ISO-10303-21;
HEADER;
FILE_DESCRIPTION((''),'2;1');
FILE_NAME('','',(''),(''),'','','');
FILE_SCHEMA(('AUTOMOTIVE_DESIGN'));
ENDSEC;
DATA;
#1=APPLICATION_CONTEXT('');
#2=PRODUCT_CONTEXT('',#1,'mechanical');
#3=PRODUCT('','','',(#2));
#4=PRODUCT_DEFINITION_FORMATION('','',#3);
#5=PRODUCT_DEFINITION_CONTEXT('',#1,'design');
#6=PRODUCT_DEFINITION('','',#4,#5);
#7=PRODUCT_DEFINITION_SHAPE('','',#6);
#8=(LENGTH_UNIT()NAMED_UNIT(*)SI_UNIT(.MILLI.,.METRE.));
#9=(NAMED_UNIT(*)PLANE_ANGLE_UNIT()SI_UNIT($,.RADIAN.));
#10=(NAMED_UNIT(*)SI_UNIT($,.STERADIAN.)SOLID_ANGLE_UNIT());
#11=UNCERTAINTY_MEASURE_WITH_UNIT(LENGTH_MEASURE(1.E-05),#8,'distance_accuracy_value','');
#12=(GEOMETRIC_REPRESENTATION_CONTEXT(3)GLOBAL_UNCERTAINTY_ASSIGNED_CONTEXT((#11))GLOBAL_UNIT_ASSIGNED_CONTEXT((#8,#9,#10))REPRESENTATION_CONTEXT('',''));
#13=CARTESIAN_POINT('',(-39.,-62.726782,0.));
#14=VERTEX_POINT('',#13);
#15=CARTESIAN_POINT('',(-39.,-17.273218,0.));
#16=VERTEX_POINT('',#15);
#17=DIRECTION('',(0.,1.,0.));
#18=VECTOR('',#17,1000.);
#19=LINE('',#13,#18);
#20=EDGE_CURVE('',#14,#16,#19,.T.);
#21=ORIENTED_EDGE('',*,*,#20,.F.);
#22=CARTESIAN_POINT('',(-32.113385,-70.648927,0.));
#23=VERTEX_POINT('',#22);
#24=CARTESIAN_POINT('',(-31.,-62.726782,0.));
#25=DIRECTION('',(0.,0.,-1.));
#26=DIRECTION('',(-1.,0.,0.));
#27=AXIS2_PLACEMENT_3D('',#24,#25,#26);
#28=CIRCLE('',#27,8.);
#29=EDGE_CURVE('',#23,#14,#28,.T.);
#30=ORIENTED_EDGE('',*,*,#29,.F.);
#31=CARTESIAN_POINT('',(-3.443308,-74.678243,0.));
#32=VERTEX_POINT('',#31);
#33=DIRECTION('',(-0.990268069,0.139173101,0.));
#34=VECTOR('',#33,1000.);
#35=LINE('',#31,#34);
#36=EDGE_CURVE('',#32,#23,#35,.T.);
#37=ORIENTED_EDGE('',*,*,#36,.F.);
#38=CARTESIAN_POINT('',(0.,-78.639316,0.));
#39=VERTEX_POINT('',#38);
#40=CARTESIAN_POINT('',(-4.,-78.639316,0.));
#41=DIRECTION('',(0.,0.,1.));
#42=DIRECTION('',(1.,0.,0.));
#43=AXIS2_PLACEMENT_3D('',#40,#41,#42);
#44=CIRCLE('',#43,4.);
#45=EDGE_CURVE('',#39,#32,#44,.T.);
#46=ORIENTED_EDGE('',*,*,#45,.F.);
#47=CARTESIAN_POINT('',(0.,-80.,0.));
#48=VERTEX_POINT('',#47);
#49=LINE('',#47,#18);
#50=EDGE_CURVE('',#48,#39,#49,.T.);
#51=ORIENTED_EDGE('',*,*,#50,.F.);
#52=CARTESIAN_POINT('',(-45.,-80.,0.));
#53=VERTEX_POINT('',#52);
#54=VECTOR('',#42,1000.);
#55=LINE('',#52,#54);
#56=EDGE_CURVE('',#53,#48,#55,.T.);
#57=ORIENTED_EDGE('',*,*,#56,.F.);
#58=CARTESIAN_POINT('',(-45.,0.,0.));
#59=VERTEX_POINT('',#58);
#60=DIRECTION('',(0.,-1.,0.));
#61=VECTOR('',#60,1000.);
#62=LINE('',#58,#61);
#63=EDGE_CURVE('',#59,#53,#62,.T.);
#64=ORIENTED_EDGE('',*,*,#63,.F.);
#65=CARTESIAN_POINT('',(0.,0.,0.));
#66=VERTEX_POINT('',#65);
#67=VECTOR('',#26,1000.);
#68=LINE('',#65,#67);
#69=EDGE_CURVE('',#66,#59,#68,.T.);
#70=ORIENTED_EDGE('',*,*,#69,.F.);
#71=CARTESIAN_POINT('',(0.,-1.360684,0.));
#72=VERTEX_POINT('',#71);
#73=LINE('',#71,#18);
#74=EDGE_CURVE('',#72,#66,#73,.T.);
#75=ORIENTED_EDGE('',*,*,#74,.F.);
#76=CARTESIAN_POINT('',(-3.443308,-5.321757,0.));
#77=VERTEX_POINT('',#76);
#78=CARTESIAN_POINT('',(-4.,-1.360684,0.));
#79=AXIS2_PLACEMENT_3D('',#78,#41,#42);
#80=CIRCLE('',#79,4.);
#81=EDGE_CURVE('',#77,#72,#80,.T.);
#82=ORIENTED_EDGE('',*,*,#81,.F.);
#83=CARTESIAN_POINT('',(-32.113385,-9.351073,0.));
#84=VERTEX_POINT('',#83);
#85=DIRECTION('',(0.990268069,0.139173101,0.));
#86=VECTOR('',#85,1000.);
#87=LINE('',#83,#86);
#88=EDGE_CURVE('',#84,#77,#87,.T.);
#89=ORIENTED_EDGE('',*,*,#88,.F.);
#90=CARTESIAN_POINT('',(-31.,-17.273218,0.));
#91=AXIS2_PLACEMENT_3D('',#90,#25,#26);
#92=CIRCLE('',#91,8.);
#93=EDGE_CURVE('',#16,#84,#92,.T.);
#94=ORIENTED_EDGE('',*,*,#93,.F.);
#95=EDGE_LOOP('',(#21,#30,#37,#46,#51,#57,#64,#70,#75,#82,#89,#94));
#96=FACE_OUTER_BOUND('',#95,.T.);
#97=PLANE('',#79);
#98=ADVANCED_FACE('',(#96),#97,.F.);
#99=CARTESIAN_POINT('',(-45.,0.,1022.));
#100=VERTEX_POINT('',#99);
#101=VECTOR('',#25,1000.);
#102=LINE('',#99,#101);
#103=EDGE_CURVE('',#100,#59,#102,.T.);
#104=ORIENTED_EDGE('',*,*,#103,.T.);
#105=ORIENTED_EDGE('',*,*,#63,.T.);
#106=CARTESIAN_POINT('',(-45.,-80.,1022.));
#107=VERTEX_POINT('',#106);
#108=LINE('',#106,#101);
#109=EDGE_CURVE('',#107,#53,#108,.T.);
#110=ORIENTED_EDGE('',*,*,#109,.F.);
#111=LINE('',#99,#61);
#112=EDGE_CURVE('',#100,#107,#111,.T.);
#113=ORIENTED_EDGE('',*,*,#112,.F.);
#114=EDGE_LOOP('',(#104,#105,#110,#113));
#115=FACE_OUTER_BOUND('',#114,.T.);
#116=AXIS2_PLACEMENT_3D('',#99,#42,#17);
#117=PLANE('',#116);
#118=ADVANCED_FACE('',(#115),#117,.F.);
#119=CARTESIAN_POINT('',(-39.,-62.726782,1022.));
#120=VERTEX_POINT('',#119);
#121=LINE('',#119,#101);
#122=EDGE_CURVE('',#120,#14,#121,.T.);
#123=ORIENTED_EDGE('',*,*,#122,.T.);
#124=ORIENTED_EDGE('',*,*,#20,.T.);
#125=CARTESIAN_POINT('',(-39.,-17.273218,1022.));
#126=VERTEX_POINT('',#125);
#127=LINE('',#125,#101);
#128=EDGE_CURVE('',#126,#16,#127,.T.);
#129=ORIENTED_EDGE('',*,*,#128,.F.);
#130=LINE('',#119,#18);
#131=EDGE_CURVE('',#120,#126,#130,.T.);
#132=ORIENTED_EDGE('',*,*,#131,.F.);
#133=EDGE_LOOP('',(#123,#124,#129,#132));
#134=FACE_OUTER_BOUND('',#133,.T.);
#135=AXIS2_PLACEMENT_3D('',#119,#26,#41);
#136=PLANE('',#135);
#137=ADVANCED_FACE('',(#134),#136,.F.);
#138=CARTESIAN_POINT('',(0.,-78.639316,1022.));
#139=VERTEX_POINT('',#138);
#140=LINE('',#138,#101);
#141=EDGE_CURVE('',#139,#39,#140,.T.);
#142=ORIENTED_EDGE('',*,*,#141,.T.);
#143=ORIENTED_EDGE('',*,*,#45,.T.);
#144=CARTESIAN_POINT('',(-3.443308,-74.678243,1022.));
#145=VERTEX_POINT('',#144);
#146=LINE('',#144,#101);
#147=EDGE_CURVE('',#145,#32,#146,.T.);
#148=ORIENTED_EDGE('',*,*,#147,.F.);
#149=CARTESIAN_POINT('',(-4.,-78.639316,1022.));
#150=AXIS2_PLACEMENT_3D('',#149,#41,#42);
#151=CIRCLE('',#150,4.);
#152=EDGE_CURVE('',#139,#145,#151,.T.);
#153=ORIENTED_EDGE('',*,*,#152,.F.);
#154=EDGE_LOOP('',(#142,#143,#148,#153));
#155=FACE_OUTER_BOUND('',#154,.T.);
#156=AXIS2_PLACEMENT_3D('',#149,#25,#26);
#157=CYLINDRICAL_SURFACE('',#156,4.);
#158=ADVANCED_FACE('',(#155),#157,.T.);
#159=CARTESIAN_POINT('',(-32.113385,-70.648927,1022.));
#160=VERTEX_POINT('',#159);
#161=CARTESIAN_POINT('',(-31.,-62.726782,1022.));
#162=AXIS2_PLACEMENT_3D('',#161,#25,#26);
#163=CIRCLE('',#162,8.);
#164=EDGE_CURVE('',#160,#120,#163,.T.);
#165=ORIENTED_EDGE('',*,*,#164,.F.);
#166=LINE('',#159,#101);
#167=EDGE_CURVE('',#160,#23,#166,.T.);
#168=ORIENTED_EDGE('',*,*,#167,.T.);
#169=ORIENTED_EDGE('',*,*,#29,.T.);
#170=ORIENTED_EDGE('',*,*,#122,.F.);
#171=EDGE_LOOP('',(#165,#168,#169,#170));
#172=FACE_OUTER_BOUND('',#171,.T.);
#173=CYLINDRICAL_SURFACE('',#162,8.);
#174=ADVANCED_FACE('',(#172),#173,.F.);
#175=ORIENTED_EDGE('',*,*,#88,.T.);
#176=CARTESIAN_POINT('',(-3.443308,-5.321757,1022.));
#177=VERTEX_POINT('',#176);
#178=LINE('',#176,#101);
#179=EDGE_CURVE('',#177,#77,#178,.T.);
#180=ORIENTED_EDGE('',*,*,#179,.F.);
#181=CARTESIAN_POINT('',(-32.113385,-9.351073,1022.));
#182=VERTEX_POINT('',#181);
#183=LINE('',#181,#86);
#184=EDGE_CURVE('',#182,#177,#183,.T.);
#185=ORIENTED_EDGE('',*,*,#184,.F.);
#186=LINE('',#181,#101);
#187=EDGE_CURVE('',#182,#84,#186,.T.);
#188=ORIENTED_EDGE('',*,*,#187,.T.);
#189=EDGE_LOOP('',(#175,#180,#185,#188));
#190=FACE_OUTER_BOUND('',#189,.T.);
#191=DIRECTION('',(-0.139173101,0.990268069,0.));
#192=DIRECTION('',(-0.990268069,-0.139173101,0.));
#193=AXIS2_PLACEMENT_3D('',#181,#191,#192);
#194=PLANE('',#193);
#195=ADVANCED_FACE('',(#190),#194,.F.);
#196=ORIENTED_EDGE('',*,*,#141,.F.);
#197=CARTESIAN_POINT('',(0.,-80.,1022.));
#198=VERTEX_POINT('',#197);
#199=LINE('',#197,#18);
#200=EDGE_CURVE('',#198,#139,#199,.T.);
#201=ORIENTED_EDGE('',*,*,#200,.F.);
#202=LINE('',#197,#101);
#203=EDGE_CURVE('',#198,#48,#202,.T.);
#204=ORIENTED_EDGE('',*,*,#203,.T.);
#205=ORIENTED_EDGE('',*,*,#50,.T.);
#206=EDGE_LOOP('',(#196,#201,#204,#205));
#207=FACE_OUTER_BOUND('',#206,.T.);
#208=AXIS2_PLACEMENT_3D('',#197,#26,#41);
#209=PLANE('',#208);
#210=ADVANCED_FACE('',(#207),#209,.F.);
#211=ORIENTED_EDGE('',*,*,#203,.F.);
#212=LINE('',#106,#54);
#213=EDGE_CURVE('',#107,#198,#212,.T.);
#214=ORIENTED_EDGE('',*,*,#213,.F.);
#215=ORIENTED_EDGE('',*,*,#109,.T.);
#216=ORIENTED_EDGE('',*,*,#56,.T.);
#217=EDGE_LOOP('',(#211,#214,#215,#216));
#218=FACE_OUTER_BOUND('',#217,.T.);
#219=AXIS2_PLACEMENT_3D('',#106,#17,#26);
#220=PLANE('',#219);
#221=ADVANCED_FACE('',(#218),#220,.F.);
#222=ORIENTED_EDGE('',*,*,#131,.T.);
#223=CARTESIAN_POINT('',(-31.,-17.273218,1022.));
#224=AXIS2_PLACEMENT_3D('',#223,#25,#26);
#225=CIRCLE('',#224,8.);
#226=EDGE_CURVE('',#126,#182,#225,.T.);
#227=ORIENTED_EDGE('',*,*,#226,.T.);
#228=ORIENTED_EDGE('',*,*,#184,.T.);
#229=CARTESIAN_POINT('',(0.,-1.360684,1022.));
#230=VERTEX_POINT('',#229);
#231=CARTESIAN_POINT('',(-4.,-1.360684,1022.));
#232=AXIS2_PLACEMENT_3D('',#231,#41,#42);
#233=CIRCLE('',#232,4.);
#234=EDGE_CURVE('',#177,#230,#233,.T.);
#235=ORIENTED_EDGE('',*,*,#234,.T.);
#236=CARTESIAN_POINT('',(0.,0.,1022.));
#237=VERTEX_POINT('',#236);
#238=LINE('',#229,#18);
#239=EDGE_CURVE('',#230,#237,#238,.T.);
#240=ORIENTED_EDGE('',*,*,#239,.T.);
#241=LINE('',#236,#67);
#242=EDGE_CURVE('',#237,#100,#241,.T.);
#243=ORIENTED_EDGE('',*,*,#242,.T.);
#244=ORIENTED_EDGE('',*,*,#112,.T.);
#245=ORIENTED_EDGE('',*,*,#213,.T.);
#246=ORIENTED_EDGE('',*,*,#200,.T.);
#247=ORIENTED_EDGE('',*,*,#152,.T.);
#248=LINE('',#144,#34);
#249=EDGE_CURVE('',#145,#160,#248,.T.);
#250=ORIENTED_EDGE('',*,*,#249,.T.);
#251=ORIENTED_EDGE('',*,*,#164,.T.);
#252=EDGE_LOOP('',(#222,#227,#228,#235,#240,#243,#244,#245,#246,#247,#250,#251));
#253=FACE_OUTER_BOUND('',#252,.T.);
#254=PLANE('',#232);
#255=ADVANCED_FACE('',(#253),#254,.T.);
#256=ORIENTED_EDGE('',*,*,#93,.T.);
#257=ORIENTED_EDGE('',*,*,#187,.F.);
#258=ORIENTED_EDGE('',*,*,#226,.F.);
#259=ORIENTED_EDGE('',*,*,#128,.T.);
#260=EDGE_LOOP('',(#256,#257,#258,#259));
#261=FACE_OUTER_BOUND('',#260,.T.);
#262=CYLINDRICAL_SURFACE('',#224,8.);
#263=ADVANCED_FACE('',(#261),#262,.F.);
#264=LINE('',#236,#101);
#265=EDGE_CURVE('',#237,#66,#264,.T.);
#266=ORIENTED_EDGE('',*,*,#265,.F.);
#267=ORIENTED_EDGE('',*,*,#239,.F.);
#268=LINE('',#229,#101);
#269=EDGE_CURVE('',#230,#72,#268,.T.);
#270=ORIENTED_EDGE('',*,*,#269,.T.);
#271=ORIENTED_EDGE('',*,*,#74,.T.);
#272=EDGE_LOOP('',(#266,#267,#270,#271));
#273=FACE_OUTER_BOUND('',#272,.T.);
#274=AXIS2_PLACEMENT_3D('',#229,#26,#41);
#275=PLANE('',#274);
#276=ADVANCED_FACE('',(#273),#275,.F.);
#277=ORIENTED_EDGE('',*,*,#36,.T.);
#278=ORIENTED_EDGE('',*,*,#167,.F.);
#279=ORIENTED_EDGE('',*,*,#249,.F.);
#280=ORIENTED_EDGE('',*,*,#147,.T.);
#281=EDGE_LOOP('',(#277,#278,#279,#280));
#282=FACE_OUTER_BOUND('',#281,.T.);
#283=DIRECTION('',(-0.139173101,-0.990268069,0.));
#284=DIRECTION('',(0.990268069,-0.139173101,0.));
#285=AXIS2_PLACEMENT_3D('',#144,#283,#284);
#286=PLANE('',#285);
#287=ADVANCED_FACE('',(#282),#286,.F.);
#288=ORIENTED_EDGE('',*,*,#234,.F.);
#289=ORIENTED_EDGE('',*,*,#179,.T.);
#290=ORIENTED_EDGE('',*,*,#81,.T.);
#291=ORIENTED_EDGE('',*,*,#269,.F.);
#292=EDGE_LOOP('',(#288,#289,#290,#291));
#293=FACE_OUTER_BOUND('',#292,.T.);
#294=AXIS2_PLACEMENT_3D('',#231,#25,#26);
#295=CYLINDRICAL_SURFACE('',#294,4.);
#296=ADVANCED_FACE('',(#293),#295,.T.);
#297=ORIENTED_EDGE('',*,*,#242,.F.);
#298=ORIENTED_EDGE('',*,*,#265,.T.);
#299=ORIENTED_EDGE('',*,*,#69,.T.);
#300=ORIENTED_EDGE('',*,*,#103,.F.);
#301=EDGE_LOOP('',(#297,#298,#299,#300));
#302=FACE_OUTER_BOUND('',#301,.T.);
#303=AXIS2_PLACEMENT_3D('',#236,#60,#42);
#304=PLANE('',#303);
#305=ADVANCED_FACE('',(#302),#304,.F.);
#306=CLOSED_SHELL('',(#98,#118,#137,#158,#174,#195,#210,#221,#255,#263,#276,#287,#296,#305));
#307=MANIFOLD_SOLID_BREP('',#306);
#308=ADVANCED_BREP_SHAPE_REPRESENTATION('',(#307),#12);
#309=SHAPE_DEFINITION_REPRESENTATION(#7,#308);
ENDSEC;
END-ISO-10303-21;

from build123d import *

# Parameters (mm, degrees)
BOSS_EXTRUDE1_DEPTH = 1022


with BuildPart() as part:
    # Sketch1 → Boss-Extrude1 (new body)
    with BuildSketch(Plane.XY):
        with BuildLine():
            Line((0, 0), (-45, 0))
            Line((-45, 0), (-45, -80))
            Line((-45, -80), (0, -80))
            Line((0, -80), (0, -78.639315732))
            ThreePointArc((0, -78.639315732), (-0.981161679, -76.015079616), (-3.443307596, -74.678243457))
            Line((-3.443307596, -74.678243457), (-32.113384808, -70.648926875))
            ThreePointArc((-32.113384808, -70.648926875), (-37.037676642, -67.975254557), (-39, -62.726782325))
            Line((-39, -62.726782325), (-39, -17.273217675))
            ThreePointArc((-39, -17.273217675), (-37.037676642, -12.024745443), (-32.113384808, -9.351073125))
            Line((-32.113384808, -9.351073125), (-3.443307596, -5.321756543))
            ThreePointArc((-3.443307596, -5.321756543), (-0.981161679, -3.984920384), (0, -1.360684268))
            Line((0, -1.360684268), (0, 0))
        make_face()
    extrude(amount=BOSS_EXTRUDE1_DEPTH)


solid = part.part
